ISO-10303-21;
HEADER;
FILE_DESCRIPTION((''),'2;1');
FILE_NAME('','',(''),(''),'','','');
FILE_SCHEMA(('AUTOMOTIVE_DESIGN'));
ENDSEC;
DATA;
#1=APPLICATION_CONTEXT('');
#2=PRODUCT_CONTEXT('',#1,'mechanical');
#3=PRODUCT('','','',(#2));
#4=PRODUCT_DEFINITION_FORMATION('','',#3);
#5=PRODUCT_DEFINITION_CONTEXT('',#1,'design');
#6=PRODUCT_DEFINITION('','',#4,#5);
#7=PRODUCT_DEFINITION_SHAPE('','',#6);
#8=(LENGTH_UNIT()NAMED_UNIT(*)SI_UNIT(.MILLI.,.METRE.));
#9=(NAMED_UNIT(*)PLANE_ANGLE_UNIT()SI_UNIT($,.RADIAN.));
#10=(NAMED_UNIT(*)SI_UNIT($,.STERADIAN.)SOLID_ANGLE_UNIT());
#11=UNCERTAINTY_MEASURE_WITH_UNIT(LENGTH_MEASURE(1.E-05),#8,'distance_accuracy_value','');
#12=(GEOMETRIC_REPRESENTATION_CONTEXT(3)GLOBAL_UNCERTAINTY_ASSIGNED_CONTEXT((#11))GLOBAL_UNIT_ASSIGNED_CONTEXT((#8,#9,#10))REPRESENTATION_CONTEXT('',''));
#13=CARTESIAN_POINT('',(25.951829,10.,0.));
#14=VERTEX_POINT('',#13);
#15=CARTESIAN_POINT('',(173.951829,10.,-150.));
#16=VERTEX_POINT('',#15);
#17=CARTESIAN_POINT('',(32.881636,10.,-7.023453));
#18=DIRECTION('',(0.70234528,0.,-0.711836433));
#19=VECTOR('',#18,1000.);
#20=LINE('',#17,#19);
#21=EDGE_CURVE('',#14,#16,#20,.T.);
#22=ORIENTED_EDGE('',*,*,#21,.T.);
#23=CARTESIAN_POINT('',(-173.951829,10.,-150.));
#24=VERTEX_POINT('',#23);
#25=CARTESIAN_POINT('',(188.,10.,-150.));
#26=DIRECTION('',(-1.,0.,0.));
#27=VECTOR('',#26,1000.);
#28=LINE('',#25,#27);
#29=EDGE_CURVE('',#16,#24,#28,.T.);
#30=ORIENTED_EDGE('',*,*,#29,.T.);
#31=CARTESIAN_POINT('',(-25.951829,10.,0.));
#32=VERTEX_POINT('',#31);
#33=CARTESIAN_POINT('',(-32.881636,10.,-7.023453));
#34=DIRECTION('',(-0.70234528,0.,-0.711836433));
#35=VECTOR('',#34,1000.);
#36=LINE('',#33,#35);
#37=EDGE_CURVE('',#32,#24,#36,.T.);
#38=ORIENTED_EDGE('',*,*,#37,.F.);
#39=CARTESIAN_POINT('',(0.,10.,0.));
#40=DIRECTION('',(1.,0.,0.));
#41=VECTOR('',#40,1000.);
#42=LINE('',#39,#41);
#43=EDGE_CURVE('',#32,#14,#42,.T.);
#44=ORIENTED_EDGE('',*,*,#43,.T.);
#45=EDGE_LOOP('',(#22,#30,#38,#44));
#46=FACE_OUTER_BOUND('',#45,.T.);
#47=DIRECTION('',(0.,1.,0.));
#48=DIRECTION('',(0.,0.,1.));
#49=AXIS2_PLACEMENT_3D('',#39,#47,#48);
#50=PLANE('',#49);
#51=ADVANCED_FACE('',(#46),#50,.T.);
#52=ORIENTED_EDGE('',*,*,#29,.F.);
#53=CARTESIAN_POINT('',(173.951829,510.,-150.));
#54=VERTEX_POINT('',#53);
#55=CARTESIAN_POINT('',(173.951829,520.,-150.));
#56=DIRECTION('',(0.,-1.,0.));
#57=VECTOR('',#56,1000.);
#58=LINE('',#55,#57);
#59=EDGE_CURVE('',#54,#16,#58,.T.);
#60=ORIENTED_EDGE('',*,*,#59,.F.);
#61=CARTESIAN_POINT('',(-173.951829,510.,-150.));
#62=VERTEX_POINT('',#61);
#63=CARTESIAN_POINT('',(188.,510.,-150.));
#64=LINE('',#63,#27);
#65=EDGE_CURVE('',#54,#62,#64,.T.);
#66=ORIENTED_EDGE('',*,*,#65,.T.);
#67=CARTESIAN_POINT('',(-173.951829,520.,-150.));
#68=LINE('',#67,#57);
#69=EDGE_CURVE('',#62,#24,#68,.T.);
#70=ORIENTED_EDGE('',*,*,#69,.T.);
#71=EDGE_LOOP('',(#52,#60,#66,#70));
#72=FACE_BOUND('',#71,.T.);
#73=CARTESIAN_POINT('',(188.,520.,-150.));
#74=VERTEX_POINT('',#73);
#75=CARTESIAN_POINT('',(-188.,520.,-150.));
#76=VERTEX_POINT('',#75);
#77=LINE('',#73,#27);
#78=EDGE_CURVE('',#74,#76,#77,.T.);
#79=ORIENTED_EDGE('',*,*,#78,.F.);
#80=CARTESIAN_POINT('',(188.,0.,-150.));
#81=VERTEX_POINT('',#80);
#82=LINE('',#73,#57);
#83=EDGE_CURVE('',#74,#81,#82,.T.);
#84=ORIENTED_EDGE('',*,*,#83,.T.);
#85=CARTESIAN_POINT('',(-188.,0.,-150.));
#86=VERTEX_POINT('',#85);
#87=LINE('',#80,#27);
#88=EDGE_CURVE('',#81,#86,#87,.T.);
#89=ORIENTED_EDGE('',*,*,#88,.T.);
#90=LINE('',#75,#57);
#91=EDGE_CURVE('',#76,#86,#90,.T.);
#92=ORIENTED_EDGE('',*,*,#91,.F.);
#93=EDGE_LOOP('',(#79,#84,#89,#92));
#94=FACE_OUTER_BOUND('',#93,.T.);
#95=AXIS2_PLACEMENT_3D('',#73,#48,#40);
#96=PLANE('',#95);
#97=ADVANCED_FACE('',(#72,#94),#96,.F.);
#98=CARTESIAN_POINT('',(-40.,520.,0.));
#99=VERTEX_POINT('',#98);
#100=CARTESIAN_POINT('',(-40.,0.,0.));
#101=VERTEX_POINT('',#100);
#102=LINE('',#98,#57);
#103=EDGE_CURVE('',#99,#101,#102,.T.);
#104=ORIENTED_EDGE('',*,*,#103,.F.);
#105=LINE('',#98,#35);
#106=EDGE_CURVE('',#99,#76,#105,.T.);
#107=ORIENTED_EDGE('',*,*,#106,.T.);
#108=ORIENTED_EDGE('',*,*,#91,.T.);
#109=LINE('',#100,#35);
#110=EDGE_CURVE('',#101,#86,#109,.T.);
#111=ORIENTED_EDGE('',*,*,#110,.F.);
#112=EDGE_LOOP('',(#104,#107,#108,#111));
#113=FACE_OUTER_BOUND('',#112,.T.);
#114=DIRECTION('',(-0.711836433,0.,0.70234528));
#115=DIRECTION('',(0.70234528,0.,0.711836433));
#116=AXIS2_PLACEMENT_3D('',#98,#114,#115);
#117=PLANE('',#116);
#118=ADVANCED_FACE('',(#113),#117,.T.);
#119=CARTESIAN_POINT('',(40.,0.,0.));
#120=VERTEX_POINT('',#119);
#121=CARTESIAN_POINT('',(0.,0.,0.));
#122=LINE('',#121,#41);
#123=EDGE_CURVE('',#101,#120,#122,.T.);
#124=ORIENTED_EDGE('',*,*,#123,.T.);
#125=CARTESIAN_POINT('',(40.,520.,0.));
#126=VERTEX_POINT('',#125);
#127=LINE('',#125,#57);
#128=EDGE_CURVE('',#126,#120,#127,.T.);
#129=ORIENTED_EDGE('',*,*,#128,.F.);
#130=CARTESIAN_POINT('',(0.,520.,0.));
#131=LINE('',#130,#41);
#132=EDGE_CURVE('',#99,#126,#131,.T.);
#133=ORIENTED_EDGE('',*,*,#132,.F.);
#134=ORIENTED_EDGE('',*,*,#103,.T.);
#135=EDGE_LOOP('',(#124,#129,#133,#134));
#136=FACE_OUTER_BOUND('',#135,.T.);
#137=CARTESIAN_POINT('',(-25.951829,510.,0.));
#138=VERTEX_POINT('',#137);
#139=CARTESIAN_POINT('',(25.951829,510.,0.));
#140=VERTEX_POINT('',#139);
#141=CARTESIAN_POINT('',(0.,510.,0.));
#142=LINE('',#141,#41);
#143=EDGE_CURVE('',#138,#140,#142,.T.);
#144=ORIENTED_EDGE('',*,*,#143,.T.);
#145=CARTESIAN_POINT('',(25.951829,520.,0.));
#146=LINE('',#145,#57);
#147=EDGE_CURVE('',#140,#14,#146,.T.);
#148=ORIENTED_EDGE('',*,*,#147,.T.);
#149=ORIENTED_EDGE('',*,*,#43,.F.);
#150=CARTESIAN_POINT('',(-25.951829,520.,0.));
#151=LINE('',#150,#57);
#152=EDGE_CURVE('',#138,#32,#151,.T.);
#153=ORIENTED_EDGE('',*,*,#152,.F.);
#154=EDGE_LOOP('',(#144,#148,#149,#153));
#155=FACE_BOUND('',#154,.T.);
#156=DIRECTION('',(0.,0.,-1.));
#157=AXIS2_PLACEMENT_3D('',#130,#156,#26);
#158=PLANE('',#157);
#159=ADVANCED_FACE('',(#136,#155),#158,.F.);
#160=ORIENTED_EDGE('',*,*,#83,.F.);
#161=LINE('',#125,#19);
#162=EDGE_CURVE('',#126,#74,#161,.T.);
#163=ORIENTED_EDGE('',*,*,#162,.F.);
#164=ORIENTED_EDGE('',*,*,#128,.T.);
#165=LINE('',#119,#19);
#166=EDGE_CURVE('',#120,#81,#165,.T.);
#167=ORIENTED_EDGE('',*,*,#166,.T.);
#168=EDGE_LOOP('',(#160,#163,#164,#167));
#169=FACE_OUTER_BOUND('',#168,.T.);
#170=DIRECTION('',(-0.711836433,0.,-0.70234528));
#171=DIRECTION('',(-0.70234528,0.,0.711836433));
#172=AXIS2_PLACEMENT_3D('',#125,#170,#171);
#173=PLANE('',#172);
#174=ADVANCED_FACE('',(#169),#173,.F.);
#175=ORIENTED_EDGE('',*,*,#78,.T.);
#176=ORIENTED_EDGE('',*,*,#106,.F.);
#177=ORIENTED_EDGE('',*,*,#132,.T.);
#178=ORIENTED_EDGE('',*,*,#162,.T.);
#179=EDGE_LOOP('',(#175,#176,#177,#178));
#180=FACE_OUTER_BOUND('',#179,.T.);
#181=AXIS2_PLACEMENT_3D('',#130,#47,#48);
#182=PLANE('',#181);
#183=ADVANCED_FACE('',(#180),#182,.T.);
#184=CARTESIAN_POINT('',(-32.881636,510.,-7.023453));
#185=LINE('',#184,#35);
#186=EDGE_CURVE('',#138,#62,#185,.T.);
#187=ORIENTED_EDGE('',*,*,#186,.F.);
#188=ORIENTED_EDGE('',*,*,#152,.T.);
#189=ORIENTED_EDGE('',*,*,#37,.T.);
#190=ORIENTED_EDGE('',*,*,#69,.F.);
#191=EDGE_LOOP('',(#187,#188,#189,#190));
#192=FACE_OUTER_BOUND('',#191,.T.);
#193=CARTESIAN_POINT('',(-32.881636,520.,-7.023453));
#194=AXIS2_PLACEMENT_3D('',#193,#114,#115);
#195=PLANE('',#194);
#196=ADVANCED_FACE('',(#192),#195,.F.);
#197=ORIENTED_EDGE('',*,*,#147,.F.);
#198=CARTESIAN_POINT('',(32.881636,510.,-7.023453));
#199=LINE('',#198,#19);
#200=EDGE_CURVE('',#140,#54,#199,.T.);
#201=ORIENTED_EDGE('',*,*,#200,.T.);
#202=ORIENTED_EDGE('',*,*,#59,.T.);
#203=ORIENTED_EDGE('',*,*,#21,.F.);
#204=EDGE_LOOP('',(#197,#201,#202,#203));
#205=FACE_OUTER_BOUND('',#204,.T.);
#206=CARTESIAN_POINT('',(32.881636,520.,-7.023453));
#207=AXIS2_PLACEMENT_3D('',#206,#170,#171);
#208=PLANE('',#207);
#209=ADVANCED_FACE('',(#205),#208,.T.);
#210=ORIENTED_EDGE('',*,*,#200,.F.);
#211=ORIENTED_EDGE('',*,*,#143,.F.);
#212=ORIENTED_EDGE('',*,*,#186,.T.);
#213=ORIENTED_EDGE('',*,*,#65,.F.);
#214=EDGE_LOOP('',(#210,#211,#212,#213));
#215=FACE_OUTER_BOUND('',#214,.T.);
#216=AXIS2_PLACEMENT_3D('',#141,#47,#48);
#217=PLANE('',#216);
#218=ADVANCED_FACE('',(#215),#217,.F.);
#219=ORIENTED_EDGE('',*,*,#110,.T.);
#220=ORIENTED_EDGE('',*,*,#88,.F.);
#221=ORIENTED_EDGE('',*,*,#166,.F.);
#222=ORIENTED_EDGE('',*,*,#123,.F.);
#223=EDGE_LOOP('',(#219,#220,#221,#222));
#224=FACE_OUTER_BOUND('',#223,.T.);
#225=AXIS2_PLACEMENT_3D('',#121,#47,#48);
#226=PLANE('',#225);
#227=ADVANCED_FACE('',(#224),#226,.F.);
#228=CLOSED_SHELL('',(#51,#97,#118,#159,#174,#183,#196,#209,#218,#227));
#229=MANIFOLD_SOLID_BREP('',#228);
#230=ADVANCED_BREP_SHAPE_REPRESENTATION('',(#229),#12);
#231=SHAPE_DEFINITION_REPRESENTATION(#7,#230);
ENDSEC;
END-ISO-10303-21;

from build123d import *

# Parameters (mm, degrees)
BOSS_EXTRUDE1_DEPTH = 520
SHELL1_T            = -10


with BuildPart() as part:
    # Sketch1 → Boss-Extrude1 (new body)
    with BuildSketch(Plane(origin=(0, 0, 0), x_dir=(1, 0, 0), z_dir=(0, 1, 0))):
        Polygon((0, 0), (40, 0), (188, 150), (0, 150), align=None)
    boss_extrude1 = extrude(amount=BOSS_EXTRUDE1_DEPTH)

    # Mirror1: Boss-Extrude1 across plane
    add(boss_extrude1.mirror(Plane(origin=(0, 520, 0), x_dir=(0, 0, 1), z_dir=(1, 0, 0))))

    # Shell1
    shell1_openings = [part.faces().sort_by_distance(p)[0] for p in [
        (0, 260, -150),
        (0, 260, 0),
    ]]
    offset(amount=SHELL1_T, openings=shell1_openings, kind=Kind.INTERSECTION)


solid = part.part
